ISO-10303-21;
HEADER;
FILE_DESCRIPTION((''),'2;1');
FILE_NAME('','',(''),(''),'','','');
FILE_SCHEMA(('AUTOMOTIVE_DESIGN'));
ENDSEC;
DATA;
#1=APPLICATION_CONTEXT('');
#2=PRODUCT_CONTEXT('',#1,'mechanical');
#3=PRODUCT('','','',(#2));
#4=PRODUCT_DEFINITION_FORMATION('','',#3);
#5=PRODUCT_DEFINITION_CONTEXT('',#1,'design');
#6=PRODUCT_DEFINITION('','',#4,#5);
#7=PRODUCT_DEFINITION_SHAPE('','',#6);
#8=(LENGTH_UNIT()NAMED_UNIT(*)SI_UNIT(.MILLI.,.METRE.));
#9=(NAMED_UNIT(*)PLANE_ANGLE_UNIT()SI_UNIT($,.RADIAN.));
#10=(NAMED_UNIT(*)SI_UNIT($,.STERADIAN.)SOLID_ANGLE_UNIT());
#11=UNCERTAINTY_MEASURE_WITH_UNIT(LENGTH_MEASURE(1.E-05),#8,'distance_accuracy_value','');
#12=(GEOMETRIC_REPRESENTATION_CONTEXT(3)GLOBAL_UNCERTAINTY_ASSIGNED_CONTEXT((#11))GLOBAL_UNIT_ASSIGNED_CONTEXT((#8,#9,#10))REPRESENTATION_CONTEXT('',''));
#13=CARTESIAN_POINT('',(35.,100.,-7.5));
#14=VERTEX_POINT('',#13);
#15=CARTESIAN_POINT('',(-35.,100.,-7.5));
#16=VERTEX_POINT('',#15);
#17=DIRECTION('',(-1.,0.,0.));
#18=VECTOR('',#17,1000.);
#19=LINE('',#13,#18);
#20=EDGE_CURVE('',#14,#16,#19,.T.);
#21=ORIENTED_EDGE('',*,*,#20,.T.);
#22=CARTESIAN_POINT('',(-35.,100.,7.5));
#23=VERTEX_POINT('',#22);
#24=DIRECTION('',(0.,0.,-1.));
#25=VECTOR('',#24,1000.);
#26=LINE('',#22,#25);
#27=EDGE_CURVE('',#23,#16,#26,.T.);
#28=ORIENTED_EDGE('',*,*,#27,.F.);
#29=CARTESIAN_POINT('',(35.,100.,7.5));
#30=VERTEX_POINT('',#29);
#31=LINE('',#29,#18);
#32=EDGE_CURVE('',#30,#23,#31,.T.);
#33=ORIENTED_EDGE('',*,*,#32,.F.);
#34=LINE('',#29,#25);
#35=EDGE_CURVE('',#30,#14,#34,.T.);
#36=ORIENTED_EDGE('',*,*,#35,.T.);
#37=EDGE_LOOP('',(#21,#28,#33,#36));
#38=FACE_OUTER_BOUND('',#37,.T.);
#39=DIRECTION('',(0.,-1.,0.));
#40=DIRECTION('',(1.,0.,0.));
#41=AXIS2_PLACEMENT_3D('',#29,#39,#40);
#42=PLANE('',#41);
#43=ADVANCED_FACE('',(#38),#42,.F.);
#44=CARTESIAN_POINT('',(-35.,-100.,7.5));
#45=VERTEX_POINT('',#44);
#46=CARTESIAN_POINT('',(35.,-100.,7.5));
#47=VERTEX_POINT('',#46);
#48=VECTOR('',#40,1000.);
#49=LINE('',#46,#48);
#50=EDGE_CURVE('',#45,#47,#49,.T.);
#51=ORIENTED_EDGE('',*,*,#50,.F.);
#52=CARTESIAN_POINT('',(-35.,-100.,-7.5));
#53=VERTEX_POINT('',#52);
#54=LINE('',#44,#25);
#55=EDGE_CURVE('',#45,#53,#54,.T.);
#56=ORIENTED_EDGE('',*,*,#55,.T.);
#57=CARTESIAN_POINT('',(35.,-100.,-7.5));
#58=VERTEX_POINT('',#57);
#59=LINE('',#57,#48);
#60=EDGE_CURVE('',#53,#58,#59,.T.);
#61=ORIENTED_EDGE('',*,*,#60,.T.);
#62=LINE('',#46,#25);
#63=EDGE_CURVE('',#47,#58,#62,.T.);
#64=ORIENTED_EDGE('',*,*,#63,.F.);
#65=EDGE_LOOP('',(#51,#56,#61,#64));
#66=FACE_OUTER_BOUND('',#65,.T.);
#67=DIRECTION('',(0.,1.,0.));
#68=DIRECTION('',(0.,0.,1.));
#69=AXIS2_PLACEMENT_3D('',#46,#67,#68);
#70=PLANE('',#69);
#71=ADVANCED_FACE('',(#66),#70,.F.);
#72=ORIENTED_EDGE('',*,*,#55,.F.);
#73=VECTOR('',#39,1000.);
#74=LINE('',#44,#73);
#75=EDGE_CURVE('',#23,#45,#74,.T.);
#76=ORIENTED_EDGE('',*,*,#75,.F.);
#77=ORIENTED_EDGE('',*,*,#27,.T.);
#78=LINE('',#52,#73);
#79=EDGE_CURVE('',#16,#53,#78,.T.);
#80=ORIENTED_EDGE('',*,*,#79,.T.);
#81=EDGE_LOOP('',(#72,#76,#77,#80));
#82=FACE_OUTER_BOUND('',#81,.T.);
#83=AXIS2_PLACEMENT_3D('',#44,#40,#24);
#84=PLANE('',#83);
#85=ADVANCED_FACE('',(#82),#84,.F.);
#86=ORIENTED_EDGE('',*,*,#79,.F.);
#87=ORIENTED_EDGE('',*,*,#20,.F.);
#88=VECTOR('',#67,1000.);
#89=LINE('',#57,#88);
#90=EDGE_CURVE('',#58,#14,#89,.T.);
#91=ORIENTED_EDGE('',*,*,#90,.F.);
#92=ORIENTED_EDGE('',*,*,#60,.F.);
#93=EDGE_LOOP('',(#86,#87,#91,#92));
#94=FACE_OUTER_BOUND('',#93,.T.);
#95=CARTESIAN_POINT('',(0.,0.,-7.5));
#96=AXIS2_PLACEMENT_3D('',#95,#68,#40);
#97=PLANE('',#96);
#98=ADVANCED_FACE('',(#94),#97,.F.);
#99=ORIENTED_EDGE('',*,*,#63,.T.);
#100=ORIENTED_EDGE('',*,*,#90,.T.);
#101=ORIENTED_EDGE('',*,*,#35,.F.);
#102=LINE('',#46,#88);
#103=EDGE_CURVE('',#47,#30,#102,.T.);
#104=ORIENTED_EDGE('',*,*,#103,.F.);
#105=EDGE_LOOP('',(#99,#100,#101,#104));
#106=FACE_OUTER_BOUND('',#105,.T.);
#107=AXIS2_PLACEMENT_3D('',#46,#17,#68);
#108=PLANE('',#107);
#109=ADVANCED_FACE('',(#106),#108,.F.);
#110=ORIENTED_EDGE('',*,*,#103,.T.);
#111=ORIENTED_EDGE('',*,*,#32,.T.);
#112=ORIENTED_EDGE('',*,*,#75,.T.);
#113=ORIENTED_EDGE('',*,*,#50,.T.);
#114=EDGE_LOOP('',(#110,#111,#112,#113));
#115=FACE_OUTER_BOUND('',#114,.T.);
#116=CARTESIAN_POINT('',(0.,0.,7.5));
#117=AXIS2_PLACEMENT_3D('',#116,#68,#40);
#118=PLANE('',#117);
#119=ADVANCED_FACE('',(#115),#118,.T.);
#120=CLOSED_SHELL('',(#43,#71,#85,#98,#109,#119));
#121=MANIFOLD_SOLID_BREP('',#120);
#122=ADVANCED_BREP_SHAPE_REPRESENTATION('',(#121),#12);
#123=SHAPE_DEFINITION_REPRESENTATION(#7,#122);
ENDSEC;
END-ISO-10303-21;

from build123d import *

# Parameters (mm, degrees)
SKETCH1_W           = 70
SKETCH1_H           = 200
BOSS_EXTRUDE1_DEPTH = 7.5


with BuildPart() as part:
    # Sketch1 → Boss-Extrude1 (new, symmetric)
    with BuildSketch(Plane.XY):
        Rectangle(SKETCH1_W, SKETCH1_H)
    extrude(amount=BOSS_EXTRUDE1_DEPTH, both=True)


solid = part.part
